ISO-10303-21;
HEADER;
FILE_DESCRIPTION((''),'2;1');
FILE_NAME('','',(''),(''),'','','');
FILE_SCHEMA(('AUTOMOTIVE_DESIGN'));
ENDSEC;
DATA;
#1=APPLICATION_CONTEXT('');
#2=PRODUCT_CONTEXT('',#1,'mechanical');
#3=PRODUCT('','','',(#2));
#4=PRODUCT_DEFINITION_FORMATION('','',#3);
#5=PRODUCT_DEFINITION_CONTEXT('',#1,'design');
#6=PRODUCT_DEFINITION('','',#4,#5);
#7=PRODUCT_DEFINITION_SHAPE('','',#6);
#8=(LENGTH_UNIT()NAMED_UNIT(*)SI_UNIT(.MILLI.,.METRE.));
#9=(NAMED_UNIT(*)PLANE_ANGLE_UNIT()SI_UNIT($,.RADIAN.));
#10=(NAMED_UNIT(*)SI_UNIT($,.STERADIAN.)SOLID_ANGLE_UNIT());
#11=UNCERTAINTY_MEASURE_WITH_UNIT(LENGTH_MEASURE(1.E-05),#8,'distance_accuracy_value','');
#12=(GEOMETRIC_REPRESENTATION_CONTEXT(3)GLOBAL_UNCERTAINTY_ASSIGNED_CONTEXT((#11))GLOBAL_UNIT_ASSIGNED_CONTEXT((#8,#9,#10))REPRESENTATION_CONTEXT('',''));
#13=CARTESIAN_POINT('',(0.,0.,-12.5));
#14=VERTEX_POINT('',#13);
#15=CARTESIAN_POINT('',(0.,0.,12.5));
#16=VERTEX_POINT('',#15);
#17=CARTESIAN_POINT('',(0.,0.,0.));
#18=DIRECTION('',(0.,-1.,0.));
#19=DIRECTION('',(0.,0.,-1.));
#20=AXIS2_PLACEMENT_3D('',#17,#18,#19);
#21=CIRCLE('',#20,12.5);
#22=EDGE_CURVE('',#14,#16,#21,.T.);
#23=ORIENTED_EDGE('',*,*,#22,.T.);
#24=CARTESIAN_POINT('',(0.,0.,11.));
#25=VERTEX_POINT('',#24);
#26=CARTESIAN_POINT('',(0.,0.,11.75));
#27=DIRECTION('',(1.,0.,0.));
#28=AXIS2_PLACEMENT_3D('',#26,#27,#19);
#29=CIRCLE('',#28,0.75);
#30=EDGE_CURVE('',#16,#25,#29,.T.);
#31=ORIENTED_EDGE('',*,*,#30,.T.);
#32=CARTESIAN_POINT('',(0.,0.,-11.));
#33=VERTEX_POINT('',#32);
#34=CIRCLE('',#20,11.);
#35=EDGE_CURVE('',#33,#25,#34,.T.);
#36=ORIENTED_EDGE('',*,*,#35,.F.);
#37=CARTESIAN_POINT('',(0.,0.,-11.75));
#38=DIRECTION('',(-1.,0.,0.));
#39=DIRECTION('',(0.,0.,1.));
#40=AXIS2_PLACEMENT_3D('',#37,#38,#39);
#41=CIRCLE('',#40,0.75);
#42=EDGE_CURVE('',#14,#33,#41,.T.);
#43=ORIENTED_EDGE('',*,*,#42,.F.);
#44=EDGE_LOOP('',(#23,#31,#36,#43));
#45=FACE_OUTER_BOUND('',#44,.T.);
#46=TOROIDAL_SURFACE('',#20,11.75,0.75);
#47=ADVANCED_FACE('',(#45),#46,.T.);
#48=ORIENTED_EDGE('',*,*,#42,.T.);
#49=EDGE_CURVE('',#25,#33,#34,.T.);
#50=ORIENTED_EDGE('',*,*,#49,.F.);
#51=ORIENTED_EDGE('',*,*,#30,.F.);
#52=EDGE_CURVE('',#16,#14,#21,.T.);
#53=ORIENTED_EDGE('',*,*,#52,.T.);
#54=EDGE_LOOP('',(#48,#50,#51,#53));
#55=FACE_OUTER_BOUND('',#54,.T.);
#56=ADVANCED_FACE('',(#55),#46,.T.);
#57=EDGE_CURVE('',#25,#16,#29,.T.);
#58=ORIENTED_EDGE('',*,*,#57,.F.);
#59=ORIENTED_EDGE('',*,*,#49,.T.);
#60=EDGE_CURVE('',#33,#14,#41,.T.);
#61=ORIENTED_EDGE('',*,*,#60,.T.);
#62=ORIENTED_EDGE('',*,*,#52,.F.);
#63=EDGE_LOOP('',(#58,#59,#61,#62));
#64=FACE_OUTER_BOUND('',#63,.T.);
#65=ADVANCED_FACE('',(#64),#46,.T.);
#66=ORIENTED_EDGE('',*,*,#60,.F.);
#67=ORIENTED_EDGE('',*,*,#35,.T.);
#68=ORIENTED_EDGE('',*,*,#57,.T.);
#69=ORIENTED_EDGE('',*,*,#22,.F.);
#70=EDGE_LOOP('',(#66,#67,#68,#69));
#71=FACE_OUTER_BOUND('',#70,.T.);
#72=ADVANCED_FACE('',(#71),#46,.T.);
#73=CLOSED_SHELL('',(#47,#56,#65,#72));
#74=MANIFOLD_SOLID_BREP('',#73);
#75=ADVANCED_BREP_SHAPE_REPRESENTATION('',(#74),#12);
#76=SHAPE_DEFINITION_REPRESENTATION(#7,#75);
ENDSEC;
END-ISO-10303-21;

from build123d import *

# Parameters (mm, degrees)
SKETCH_1_R = 0.75


with BuildPart() as part:
    # 草图1 → 旋转1 (revolve)
    with BuildSketch(Plane.XY, mode=Mode.PRIVATE) as revolve_1_sk:
        with Locations((-11.75, 0)):
            Circle(SKETCH_1_R)
    revolve(revolve_1_sk.sketch.rotate(Axis((0, 0, 0), (0, 1, 0)), 270), axis=Axis((0, 0, 0), (0, 1, 0)))


solid = part.part
